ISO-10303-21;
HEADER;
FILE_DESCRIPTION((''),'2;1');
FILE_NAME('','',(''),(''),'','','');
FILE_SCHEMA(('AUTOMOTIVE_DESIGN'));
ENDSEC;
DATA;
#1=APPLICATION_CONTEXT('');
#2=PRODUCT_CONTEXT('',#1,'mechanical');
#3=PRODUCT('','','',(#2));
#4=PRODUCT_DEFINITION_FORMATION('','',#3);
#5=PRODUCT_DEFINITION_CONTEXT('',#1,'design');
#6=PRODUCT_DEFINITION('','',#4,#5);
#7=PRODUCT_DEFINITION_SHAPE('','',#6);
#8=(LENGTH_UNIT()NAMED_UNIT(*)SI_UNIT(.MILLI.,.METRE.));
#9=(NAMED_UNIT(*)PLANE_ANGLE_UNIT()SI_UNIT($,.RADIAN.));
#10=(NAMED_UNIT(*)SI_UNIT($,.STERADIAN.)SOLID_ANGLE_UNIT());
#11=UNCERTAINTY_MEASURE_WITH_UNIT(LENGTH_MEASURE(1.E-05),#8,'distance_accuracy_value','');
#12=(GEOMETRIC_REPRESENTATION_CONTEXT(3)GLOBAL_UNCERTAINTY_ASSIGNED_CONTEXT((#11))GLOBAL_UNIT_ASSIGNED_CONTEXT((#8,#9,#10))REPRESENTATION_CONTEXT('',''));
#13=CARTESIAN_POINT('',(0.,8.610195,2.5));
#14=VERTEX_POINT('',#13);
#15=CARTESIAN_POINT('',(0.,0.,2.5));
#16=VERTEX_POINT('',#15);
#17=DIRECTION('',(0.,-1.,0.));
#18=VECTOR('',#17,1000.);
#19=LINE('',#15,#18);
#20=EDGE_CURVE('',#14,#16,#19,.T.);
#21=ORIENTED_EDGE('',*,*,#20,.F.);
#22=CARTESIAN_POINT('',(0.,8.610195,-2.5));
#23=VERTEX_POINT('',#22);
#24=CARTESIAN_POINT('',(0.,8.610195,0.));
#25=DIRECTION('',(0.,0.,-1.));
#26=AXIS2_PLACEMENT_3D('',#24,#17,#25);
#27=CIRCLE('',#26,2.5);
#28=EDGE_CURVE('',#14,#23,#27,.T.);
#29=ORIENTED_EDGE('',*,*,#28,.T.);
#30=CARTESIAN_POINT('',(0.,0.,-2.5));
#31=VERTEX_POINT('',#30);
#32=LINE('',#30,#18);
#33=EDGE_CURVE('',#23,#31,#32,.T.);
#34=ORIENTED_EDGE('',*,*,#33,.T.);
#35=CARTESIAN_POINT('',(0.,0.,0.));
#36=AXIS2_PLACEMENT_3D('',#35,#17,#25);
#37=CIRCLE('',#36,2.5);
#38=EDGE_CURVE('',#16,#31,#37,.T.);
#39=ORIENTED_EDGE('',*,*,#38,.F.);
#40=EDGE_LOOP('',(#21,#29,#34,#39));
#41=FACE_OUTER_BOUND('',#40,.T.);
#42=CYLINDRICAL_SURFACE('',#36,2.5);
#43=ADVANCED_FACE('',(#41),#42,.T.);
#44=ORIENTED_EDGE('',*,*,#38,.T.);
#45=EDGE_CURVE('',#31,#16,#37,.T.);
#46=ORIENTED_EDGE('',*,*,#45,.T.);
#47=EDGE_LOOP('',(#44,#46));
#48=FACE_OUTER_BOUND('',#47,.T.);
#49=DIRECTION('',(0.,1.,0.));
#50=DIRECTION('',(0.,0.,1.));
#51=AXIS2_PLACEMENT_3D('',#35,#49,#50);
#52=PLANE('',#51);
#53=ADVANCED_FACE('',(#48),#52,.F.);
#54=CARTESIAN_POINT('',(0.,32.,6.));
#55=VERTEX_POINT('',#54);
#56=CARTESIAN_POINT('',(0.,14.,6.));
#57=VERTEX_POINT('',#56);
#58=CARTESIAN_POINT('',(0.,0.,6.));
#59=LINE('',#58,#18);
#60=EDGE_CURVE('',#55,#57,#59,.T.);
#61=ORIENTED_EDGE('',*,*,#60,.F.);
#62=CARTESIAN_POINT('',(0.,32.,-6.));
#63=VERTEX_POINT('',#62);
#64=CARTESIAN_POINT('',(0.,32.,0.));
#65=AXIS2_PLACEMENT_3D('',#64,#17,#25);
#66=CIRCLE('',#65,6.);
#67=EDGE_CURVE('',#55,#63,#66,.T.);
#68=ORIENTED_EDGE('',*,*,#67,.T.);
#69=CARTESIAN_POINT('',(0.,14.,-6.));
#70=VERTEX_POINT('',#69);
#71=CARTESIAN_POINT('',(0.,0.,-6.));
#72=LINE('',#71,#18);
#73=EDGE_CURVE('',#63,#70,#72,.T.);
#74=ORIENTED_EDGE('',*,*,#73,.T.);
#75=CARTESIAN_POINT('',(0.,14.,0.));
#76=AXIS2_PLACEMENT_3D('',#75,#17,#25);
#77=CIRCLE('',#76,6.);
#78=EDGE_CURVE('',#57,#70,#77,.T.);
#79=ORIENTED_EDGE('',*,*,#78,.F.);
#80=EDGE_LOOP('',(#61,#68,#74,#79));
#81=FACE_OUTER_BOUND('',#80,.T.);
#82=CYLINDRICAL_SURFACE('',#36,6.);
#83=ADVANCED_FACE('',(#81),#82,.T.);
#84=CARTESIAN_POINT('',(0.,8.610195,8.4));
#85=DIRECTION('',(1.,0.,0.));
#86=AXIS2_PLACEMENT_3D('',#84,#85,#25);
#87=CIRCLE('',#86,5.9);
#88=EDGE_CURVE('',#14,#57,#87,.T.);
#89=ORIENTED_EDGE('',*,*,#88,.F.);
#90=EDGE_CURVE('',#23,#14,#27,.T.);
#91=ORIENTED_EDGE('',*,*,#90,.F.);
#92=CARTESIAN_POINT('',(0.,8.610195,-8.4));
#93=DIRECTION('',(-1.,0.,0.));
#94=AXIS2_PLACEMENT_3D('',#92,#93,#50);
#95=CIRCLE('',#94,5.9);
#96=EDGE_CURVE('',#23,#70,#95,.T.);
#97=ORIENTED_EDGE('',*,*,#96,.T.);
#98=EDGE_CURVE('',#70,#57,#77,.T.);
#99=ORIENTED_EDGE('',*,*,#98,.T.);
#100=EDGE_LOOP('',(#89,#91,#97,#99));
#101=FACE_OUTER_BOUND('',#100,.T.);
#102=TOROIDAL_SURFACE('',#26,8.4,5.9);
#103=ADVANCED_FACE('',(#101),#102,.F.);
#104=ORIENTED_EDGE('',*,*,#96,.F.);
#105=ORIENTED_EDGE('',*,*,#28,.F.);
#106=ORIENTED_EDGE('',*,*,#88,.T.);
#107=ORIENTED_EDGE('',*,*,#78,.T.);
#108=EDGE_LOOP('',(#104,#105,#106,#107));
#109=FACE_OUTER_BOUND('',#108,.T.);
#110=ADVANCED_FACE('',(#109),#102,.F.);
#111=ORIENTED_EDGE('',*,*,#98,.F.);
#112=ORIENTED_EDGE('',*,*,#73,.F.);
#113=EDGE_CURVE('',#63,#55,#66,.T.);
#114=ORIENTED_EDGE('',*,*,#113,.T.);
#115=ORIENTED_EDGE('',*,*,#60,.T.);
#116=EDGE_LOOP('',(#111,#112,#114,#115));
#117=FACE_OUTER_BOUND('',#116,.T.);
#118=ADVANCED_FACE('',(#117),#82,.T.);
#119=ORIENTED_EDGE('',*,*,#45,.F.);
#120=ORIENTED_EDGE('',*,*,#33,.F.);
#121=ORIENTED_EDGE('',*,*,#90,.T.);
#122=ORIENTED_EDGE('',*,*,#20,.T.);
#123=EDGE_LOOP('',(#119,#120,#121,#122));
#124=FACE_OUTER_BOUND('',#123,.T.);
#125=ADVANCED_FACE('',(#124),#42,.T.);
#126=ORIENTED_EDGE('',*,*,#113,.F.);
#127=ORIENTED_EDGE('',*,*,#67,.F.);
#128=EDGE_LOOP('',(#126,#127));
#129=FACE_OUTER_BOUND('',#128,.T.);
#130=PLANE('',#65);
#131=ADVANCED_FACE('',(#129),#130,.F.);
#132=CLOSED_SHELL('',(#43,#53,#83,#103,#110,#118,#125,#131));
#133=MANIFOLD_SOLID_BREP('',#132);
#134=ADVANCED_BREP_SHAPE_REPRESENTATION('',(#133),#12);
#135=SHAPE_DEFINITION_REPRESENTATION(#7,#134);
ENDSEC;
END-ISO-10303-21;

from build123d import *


with BuildPart() as part:
    # Punch Profile Sketch → Punch Body Revolve (revolve)
    with BuildSketch(Plane.XY, mode=Mode.PRIVATE) as punch_body_revolve_sk:
        with BuildLine():
            Line((0, 0), (-2.5, 0))
            Line((-2.5, 0), (-2.5, 8.610194809))
            ThreePointArc((-2.5, 8.610194809), (-3.451767993, 11.823448611), (-6, 14))
            Line((-6, 14), (-6, 32))
            Line((-6, 32), (0, 32))
            Line((0, 32), (0, 0))
        make_face()
    revolve(punch_body_revolve_sk.sketch.rotate(Axis((0, 0, 0), (0, 1, 0)), 270), axis=Axis((0, 0, 0), (0, 1, 0)))


solid = part.part
